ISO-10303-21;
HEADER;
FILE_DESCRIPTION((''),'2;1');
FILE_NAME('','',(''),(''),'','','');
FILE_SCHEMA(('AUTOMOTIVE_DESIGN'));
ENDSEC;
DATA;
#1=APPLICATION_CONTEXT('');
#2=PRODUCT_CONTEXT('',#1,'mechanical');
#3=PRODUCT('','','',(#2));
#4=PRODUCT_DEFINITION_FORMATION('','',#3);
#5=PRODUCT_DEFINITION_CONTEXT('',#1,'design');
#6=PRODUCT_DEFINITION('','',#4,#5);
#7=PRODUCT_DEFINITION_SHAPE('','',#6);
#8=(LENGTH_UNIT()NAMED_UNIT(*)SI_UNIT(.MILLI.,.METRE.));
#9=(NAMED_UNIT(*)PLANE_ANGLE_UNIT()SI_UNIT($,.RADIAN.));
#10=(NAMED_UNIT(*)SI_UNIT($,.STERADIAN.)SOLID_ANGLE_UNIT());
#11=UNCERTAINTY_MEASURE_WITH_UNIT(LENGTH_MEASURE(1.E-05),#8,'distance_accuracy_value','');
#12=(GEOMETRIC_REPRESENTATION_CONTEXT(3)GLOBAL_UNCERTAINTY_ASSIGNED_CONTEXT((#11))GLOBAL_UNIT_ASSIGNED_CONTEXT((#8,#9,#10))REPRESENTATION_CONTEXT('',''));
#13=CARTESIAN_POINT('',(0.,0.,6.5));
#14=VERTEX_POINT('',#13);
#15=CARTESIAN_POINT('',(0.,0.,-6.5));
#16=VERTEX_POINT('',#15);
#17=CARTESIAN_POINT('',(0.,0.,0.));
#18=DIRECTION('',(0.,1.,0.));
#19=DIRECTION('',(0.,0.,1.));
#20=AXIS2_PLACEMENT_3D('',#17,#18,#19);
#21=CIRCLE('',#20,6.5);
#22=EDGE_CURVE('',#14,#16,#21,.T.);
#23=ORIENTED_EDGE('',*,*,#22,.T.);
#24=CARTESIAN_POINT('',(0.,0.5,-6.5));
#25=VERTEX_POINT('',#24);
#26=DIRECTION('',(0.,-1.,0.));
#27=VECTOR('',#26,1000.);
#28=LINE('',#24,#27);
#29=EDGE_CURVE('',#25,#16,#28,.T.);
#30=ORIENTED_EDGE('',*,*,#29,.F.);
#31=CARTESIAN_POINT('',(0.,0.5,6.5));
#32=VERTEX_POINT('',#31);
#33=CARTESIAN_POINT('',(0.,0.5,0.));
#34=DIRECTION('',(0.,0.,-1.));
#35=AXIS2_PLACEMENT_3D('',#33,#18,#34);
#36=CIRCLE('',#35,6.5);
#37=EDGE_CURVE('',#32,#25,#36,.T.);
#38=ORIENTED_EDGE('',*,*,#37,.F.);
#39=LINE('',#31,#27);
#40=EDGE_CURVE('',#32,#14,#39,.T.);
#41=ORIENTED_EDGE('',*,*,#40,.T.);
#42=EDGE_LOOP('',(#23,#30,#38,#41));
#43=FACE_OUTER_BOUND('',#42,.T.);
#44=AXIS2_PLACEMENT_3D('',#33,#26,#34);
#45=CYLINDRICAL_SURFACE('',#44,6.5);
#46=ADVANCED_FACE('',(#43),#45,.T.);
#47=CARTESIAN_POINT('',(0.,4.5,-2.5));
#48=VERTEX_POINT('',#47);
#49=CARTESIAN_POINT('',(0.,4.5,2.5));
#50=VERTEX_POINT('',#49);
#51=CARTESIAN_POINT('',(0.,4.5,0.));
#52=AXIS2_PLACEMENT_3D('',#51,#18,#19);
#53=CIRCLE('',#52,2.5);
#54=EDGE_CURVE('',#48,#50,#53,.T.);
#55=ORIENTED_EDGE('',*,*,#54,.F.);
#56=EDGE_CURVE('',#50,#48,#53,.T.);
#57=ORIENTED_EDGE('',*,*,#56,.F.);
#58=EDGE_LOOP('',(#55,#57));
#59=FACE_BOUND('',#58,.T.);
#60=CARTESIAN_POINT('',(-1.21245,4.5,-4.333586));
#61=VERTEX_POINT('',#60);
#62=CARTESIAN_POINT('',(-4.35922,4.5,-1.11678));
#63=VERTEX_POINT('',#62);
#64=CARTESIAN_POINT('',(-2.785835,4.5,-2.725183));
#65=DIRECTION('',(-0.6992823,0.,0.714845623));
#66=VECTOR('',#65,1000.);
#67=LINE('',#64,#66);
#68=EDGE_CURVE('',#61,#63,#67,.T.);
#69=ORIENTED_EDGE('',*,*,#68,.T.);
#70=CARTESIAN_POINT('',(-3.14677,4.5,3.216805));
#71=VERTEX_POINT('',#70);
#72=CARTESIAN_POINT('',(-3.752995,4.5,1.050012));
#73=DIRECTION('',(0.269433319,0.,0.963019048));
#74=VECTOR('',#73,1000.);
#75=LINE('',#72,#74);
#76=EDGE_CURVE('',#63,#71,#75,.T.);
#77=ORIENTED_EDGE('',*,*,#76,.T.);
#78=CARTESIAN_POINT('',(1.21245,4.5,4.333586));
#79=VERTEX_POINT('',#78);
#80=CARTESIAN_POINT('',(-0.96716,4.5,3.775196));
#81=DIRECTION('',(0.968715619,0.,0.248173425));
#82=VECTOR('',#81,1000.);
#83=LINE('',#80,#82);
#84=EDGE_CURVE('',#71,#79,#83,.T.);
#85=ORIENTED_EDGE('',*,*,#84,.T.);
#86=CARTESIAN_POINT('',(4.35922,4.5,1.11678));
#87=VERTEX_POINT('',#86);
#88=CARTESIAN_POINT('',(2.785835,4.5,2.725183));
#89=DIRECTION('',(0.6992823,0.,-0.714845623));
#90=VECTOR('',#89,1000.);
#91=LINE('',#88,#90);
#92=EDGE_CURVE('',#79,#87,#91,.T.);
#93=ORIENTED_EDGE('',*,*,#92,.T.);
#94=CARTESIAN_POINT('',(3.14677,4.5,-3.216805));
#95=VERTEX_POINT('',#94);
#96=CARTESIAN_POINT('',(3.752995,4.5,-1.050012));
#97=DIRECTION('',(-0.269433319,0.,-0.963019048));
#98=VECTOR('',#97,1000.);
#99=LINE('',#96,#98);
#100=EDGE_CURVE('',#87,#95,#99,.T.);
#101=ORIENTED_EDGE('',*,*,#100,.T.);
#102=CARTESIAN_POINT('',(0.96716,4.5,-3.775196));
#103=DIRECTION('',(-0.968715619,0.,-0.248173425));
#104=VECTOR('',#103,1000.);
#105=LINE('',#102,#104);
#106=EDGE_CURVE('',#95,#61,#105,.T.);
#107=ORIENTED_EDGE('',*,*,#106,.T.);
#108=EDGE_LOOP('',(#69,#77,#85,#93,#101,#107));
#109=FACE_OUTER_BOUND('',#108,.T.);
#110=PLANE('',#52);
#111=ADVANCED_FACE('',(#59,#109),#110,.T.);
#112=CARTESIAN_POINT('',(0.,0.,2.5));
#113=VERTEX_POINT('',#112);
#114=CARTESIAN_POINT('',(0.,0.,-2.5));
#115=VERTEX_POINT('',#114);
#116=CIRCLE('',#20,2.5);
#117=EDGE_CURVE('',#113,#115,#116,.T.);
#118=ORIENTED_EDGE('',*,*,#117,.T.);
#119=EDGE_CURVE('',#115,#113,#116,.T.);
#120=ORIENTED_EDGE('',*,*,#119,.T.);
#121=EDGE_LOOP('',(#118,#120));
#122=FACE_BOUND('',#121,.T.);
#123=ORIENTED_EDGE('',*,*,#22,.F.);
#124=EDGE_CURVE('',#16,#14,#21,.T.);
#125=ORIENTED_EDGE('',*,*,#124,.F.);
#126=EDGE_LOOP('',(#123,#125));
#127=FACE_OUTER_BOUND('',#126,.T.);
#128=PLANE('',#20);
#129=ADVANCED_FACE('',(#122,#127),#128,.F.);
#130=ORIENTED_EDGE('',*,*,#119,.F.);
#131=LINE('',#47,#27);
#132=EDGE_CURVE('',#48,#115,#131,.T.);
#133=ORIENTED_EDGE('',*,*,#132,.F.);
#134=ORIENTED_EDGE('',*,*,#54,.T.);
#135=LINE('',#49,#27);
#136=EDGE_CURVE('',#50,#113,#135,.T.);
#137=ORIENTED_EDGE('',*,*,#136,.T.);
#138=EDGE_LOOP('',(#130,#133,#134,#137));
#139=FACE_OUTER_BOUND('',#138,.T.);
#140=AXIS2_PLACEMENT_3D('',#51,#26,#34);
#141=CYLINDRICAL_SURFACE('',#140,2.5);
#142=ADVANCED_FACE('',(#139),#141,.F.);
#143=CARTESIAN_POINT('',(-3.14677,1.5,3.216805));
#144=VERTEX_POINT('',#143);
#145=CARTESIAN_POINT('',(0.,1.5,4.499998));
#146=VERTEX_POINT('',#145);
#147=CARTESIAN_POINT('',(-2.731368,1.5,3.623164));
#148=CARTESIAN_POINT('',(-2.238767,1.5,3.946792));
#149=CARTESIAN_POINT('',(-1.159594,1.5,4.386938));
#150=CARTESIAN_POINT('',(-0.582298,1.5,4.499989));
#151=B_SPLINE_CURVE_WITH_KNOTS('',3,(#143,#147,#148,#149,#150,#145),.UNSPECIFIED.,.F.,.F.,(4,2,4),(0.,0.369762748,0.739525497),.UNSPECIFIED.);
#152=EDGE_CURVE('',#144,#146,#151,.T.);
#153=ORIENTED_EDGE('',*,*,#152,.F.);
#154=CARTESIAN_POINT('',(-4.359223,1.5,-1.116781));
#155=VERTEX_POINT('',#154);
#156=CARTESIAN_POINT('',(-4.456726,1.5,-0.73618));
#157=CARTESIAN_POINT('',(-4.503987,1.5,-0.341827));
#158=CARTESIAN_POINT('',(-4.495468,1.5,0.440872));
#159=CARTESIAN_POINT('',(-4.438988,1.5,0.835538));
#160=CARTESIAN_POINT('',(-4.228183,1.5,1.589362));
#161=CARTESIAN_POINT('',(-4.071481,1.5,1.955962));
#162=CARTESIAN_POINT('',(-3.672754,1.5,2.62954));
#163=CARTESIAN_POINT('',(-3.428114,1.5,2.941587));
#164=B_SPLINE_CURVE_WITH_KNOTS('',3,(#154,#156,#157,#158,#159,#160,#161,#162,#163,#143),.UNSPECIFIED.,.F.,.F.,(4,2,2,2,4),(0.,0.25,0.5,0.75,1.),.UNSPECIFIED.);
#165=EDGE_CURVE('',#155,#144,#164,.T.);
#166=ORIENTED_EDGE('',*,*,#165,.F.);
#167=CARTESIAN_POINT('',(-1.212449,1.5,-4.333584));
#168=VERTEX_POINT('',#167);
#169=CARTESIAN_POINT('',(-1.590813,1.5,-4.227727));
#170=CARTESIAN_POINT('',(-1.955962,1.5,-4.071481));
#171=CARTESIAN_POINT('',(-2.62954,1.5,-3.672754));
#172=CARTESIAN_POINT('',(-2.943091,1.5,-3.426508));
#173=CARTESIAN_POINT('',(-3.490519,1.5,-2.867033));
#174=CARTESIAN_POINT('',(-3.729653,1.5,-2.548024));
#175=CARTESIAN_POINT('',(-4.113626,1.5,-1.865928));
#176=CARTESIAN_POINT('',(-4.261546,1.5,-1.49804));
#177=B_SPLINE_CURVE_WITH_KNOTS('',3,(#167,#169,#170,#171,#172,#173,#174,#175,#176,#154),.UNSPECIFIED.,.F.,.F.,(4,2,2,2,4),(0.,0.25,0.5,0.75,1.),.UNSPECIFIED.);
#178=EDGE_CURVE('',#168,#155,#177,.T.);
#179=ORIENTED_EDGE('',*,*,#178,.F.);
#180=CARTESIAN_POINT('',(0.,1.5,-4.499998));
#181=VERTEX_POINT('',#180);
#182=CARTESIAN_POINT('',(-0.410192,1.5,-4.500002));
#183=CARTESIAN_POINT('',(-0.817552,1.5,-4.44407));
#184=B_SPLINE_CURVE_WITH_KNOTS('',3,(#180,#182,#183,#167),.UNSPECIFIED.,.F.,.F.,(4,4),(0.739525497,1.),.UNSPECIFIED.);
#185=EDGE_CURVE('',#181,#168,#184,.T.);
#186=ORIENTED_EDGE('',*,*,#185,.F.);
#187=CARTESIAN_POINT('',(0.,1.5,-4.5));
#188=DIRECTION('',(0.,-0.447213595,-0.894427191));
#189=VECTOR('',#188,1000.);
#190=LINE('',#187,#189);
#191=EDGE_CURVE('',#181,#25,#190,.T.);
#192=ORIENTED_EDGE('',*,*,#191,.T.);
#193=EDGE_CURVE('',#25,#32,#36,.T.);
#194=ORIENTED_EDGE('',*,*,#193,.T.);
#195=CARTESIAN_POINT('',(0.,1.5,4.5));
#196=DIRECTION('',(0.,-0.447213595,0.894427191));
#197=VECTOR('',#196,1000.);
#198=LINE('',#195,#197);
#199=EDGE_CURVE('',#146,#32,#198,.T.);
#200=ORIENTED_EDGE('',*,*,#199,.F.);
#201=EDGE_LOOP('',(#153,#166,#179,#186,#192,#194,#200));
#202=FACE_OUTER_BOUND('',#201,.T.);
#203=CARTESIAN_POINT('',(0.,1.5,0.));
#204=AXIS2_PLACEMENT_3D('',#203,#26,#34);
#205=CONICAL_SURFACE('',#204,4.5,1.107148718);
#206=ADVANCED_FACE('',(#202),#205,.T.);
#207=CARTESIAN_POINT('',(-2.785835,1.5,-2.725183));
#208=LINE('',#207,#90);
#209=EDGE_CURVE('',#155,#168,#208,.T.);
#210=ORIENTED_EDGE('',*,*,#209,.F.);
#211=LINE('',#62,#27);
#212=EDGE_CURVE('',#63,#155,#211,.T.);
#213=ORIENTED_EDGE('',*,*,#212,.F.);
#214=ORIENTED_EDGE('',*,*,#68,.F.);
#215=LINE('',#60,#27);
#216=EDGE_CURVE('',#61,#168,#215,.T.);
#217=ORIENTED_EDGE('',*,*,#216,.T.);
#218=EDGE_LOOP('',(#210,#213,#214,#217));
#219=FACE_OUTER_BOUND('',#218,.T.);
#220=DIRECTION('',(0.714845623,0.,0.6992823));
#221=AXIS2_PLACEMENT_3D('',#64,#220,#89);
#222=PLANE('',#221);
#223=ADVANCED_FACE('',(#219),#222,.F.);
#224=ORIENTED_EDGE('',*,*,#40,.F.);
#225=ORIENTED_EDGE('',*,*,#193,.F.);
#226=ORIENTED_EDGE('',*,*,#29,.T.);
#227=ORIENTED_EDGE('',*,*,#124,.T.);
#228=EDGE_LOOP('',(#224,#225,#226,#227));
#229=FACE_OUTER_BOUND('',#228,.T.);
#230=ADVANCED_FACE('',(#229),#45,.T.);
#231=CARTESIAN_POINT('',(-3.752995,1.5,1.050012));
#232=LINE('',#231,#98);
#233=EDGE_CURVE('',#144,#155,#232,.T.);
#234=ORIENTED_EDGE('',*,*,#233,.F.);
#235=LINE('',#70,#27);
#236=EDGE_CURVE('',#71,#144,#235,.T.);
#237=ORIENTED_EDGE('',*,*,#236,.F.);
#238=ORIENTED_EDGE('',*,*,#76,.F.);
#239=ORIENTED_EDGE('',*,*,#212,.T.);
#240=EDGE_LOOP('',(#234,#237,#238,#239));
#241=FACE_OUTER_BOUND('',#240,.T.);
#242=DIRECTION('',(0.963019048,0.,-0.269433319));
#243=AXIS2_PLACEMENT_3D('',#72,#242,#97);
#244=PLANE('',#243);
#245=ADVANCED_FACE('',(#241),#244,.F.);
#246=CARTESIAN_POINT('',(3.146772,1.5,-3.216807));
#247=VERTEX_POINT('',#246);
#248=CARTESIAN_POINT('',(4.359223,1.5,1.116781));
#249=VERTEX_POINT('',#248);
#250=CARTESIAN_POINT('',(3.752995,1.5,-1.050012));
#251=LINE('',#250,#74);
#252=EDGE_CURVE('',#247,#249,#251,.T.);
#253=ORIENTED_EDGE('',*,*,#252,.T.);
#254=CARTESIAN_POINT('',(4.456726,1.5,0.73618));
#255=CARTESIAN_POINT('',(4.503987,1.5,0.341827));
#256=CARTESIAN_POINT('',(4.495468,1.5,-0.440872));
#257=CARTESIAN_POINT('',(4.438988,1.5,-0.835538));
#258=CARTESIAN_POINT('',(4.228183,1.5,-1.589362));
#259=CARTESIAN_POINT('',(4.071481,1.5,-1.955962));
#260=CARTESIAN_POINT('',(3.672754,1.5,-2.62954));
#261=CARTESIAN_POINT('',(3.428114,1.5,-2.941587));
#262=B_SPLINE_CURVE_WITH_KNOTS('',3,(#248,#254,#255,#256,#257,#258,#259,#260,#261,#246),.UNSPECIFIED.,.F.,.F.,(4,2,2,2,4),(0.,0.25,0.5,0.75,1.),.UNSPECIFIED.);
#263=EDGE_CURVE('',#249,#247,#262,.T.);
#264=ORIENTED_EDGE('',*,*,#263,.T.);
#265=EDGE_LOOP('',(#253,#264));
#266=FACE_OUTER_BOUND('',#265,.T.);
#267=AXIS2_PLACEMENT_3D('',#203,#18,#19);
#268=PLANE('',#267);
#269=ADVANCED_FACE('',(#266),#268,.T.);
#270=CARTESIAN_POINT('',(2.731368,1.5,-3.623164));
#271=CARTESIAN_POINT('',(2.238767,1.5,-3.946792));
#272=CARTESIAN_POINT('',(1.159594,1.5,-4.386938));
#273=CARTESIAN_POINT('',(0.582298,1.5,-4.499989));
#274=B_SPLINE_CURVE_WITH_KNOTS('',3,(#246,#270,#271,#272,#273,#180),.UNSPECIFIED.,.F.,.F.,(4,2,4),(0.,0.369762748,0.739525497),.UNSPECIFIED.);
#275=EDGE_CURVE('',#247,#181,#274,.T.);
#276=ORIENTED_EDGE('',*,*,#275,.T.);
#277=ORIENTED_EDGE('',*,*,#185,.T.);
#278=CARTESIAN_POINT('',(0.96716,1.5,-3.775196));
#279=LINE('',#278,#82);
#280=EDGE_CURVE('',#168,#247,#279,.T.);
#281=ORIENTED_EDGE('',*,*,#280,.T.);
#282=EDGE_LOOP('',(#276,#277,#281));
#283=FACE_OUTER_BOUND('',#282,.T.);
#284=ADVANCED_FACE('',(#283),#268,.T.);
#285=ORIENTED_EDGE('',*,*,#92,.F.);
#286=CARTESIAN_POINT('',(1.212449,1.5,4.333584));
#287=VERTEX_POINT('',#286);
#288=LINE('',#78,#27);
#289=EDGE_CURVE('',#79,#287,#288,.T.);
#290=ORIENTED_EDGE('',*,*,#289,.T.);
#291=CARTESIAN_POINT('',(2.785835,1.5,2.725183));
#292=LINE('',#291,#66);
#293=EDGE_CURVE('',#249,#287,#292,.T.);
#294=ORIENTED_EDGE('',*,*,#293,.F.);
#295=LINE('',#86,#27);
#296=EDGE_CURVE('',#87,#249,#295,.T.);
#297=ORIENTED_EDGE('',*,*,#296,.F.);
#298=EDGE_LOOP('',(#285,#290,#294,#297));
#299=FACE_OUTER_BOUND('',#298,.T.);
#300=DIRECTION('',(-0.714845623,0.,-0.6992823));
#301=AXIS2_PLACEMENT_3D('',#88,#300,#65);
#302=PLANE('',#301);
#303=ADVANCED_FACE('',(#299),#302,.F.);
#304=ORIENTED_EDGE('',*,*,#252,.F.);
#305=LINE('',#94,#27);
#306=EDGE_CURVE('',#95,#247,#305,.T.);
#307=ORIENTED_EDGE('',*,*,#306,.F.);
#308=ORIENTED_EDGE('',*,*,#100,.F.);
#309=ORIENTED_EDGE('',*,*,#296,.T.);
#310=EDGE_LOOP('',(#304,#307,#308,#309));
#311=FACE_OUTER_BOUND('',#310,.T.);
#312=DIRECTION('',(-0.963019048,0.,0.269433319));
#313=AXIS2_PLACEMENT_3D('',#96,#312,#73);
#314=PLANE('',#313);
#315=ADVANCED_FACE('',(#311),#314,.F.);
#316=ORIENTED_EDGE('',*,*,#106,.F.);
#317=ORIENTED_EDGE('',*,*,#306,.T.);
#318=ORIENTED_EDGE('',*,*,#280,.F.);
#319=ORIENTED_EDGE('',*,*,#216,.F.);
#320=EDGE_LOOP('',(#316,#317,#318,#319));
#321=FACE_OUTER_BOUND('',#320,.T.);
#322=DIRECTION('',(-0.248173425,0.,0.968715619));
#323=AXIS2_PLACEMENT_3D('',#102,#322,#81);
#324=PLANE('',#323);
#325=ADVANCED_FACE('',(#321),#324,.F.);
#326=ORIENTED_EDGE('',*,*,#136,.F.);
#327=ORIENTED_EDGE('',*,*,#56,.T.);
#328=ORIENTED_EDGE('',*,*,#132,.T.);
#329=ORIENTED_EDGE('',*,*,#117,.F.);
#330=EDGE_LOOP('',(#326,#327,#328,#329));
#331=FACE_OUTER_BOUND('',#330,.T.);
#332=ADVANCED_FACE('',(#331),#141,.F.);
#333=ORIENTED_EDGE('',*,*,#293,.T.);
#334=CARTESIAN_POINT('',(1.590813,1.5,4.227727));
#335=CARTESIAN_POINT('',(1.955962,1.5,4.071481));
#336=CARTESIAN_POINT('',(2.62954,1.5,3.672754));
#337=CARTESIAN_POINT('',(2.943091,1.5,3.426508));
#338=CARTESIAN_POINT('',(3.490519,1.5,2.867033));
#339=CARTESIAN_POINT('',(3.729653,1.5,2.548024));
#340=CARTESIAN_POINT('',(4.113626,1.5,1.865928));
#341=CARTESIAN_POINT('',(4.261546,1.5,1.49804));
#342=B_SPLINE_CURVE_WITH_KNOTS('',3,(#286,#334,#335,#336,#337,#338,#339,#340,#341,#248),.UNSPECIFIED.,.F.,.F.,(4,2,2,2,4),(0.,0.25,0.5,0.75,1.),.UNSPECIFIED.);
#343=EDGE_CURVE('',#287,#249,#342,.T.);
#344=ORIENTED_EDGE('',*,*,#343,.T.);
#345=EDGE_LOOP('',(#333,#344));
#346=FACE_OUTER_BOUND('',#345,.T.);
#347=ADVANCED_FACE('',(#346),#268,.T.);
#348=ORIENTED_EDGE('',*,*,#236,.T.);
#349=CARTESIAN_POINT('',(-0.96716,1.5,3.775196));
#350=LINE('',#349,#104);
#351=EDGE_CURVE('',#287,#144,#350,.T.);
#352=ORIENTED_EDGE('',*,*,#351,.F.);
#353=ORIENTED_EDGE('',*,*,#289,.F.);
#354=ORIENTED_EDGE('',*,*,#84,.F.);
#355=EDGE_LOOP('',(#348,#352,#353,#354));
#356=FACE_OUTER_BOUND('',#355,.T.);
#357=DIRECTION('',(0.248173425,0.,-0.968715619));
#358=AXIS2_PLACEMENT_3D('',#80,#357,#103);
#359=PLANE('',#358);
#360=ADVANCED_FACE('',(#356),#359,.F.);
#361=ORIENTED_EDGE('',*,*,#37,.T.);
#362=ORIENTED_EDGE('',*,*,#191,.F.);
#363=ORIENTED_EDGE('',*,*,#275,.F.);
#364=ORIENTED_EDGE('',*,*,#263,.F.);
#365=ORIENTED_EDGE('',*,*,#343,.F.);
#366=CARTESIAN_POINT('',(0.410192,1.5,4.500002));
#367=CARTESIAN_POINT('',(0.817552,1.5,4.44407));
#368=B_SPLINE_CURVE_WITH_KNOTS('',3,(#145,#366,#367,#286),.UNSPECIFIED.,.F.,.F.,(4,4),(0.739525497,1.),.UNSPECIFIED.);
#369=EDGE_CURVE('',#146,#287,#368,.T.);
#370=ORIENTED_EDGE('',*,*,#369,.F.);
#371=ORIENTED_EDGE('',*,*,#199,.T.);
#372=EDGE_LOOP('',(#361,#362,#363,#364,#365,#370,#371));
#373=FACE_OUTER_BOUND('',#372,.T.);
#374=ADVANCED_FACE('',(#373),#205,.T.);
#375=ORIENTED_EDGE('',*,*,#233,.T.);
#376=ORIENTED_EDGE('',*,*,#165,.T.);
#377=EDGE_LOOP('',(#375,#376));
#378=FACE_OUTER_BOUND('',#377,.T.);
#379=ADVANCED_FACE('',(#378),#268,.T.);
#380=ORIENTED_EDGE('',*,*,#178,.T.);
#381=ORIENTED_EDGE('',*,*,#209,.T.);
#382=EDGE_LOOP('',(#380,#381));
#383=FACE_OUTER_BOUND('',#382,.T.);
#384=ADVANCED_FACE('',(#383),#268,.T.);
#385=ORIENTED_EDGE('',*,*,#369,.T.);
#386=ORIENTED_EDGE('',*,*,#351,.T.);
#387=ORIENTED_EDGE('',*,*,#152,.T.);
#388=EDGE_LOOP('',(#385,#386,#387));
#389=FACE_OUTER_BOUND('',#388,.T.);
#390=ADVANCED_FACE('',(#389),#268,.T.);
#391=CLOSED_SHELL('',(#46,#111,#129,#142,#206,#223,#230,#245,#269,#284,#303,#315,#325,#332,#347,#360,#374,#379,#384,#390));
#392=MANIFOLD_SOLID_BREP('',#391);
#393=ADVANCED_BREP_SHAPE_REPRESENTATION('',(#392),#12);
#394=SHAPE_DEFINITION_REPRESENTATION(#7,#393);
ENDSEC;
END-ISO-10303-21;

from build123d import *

# Parameters (mm, degrees)
NUT_PROFILE_SKETCH_R     = 6.5
FLANGE_DISC_13_DEPTH     = 0.5
SKETCH1_5_R              = 4.5
FLANGE_COLLAR_DEPTH      = 1.5
SKETCH1_6_R              = 2.5
HEX_BODY_DEPTH           = 4.5
TAPER_LOFT_BASE_SKETCH_R = 6.5
TAPER_LOFT_TOP_SKETCH_R  = 4.5
THROUGH_START            = -4.5
BORE_SKETCH_R            = 2.5
THROUGH_BORE_DEPTH       = 4.5


with BuildPart() as part:
    # Nut Profile Sketch → Flange Disc _13 (new body)
    with BuildSketch(Plane(origin=(0, 0, 0), x_dir=(1, 0, 0), z_dir=(0, 1, 0))):
        with Locations(Location((0, 0, 0), (0, 0, 270))):
            Circle(NUT_PROFILE_SKETCH_R)
    extrude(amount=FLANGE_DISC_13_DEPTH)

    # Sketch1_5 → Flange Collar (add)
    with BuildSketch(Plane(origin=(0, 0, 0), x_dir=(1, 0, 0), z_dir=(0, 1, 0))):
        with Locations(Location((0, 0, 0), (0, 0, 270))):
            Circle(SKETCH1_5_R)
    extrude(amount=FLANGE_COLLAR_DEPTH)

    # Sketch1_6 → Hex Body (add)
    with BuildSketch(Plane(origin=(0, 0, 0), x_dir=(1, 0, 0), z_dir=(0, 1, 0))):
        Polygon((-3.14677035, -3.216805304), (1.212449938, -4.333585715), (4.359220287, -1.116780411), (3.14677035, 3.216805304), (-1.212449938, 4.333585715), (-4.359220287, 1.116780411), align=None)
        with Locations(Location((0, 0, 0), (0, 0, 270))):
            Circle(SKETCH1_6_R, mode=Mode.SUBTRACT)
    extrude(amount=HEX_BODY_DEPTH)

    # Taper Loft Base Sketch → Flange Taper Loft section 0
    with BuildSketch(Plane(origin=(0, 0.5, 0), x_dir=(1, 0, 0), z_dir=(0, 1, 0))):
        Circle(TAPER_LOFT_BASE_SKETCH_R)
    # Taper Loft Top Sketch → Flange Taper Loft section 1
    with BuildSketch(Plane(origin=(0, 1.5, 0), x_dir=(1, 0, 0), z_dir=(0, 1, 0))):
        Circle(TAPER_LOFT_TOP_SKETCH_R)
    loft()

    # Bore Sketch → Through Bore (cut)
    with BuildSketch(Plane(origin=(0, 1.5, 0), x_dir=(1, 0, 0), z_dir=(0, 1, 0)).offset(THROUGH_START)):
        with Locations(Location((0, 0, 0), (0, 0, 270))):
            Circle(BORE_SKETCH_R)
    extrude(amount=THROUGH_BORE_DEPTH, mode=Mode.SUBTRACT)


solid = part.part
